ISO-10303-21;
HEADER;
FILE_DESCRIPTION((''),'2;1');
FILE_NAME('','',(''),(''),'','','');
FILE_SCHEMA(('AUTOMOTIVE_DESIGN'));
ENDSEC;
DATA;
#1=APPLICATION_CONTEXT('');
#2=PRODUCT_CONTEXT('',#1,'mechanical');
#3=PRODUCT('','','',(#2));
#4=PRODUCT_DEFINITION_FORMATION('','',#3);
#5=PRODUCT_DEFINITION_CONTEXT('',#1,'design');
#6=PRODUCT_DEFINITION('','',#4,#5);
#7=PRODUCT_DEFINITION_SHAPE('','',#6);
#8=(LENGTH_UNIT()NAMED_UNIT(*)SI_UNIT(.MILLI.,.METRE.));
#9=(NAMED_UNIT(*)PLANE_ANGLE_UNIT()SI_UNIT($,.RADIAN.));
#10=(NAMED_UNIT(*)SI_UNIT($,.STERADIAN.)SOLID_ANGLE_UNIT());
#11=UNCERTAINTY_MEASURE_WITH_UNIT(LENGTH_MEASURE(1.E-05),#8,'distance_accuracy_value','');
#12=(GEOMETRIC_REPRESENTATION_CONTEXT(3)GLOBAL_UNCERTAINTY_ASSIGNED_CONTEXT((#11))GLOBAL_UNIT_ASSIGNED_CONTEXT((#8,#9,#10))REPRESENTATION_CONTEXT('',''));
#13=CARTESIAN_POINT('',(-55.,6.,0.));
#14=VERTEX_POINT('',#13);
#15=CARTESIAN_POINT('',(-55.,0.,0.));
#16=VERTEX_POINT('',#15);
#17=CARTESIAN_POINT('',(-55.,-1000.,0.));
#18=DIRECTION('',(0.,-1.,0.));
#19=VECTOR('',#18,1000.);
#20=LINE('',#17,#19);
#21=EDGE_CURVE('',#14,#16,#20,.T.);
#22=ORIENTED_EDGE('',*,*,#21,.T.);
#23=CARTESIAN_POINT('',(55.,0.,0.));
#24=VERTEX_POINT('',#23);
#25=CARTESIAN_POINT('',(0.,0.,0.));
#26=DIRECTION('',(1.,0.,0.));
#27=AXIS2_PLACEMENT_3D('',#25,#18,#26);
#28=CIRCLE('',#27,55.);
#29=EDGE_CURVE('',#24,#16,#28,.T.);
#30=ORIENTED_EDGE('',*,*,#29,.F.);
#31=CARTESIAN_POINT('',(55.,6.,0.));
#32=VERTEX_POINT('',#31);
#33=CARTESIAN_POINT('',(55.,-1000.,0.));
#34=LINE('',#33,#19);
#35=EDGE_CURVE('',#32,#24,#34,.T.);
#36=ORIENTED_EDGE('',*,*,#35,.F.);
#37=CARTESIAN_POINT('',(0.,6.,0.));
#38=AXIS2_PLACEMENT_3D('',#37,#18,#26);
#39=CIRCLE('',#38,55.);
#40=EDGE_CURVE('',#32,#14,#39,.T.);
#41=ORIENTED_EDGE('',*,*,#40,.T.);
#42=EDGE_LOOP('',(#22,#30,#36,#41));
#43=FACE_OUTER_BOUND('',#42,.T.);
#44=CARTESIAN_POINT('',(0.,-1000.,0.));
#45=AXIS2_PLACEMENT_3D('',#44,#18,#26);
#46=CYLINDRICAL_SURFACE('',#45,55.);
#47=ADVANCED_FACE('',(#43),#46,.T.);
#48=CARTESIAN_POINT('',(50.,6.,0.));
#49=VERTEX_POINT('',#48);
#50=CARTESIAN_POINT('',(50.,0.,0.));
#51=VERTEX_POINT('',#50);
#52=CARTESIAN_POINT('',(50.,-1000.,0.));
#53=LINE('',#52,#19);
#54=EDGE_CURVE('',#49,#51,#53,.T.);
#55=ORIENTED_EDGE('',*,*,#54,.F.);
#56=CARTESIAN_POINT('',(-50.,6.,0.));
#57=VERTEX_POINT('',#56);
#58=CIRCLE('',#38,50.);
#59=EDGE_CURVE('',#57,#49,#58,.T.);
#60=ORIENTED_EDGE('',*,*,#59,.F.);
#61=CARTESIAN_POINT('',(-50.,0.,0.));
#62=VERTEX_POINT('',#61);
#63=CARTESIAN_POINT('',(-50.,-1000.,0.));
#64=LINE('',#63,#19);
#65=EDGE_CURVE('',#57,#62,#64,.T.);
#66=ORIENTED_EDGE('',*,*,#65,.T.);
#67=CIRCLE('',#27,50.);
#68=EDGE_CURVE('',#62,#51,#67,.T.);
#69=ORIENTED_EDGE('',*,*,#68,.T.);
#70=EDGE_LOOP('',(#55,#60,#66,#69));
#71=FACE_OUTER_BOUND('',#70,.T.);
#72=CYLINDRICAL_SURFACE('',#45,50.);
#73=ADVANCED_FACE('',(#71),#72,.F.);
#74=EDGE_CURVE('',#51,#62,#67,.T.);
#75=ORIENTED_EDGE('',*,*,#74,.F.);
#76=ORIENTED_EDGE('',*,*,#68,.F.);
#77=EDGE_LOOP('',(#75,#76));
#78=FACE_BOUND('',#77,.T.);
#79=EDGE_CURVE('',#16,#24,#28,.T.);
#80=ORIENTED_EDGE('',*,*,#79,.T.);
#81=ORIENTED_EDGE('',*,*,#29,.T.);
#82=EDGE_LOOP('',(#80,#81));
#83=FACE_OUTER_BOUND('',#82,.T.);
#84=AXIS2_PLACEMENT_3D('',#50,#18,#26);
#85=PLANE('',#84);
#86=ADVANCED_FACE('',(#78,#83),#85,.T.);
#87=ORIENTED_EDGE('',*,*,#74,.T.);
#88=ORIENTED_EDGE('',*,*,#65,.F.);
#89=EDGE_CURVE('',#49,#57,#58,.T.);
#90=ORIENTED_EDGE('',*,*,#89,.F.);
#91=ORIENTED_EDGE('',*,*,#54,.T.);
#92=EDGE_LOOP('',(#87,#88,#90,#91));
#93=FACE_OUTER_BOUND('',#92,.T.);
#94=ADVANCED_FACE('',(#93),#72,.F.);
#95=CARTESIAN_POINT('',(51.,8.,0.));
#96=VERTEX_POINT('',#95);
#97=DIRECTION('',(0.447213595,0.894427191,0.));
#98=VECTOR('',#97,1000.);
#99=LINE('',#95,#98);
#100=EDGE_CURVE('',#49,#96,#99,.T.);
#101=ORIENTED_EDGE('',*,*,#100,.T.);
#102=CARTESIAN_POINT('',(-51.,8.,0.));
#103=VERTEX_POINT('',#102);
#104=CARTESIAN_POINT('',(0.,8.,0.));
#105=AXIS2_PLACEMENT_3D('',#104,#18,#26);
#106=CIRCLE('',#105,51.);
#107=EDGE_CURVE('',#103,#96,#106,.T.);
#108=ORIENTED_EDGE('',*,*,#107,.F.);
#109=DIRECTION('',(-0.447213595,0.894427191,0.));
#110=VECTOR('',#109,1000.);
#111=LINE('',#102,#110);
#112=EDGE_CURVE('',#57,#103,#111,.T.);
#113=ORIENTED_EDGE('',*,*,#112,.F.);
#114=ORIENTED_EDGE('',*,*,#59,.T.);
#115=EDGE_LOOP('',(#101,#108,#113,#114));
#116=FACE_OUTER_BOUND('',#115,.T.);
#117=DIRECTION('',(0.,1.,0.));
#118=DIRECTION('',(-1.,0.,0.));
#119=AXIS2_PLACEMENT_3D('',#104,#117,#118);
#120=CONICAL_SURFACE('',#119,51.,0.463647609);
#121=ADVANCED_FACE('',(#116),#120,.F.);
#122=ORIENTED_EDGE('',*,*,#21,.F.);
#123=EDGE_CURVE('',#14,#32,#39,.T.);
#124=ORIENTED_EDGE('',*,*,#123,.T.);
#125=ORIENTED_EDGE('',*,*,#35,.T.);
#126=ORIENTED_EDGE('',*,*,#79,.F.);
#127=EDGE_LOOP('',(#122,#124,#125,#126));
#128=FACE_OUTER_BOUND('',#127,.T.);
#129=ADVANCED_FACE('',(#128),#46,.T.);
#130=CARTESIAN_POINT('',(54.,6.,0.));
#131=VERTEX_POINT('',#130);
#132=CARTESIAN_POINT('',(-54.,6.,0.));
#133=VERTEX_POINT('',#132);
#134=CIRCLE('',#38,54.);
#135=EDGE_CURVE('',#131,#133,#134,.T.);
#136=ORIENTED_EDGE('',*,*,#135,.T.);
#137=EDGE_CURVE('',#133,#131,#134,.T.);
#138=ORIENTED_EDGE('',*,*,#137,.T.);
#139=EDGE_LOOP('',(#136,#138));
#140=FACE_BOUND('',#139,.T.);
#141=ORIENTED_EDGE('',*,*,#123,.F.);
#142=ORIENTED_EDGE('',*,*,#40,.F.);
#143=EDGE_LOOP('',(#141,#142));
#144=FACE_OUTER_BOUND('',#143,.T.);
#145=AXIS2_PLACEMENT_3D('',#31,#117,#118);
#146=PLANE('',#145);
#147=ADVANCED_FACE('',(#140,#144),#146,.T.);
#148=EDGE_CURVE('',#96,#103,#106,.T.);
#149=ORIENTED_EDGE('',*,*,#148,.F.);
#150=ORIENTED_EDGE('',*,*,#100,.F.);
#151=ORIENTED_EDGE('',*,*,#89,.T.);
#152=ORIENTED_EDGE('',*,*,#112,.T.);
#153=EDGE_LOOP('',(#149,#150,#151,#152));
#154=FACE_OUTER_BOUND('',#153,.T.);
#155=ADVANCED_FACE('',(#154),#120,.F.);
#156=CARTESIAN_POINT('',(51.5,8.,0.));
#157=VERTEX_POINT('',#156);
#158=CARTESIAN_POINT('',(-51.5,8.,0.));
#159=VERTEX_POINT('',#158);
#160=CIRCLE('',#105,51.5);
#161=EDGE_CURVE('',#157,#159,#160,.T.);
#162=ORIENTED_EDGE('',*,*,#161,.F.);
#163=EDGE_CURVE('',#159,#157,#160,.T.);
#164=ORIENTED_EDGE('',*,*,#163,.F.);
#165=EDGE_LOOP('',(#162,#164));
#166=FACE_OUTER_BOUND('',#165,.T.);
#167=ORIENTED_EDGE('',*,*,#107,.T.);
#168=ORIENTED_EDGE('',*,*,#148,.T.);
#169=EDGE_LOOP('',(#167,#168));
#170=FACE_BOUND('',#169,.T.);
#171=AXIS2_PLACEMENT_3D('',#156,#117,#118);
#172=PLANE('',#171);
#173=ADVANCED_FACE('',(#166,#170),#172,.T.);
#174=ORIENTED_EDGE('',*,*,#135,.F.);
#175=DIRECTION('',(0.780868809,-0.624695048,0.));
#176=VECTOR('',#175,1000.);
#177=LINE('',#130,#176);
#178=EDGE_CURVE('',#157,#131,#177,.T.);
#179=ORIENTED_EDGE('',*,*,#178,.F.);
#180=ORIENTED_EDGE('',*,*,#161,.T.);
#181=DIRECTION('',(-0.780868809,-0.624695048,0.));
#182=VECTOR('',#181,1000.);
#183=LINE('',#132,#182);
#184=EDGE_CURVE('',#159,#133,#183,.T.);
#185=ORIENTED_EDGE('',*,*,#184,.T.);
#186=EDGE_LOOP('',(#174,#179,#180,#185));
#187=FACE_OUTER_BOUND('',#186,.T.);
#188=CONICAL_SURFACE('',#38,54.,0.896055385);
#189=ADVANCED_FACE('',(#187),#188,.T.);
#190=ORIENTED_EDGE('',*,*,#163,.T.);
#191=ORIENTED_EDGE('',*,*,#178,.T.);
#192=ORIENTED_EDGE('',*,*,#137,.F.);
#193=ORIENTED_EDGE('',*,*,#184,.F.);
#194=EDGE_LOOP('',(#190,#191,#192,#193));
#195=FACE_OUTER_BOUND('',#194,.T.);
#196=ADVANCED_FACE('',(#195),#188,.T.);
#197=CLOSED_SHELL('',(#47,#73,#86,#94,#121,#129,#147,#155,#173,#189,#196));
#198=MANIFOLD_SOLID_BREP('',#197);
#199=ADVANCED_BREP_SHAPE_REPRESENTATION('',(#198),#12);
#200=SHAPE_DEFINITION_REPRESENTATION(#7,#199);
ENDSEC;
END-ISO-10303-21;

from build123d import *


with BuildPart() as part:
    # Sketch2 → Revolve1 (revolve)
    with BuildSketch(Plane.XY):
        Polygon((50, 0), (55, 0), (55, 6), (54, 6), (51.5, 8), (51, 8), (50, 6), align=None)
    revolve(axis=Axis((0, -1000, 0), (0, 1, 0)))


solid = part.part
